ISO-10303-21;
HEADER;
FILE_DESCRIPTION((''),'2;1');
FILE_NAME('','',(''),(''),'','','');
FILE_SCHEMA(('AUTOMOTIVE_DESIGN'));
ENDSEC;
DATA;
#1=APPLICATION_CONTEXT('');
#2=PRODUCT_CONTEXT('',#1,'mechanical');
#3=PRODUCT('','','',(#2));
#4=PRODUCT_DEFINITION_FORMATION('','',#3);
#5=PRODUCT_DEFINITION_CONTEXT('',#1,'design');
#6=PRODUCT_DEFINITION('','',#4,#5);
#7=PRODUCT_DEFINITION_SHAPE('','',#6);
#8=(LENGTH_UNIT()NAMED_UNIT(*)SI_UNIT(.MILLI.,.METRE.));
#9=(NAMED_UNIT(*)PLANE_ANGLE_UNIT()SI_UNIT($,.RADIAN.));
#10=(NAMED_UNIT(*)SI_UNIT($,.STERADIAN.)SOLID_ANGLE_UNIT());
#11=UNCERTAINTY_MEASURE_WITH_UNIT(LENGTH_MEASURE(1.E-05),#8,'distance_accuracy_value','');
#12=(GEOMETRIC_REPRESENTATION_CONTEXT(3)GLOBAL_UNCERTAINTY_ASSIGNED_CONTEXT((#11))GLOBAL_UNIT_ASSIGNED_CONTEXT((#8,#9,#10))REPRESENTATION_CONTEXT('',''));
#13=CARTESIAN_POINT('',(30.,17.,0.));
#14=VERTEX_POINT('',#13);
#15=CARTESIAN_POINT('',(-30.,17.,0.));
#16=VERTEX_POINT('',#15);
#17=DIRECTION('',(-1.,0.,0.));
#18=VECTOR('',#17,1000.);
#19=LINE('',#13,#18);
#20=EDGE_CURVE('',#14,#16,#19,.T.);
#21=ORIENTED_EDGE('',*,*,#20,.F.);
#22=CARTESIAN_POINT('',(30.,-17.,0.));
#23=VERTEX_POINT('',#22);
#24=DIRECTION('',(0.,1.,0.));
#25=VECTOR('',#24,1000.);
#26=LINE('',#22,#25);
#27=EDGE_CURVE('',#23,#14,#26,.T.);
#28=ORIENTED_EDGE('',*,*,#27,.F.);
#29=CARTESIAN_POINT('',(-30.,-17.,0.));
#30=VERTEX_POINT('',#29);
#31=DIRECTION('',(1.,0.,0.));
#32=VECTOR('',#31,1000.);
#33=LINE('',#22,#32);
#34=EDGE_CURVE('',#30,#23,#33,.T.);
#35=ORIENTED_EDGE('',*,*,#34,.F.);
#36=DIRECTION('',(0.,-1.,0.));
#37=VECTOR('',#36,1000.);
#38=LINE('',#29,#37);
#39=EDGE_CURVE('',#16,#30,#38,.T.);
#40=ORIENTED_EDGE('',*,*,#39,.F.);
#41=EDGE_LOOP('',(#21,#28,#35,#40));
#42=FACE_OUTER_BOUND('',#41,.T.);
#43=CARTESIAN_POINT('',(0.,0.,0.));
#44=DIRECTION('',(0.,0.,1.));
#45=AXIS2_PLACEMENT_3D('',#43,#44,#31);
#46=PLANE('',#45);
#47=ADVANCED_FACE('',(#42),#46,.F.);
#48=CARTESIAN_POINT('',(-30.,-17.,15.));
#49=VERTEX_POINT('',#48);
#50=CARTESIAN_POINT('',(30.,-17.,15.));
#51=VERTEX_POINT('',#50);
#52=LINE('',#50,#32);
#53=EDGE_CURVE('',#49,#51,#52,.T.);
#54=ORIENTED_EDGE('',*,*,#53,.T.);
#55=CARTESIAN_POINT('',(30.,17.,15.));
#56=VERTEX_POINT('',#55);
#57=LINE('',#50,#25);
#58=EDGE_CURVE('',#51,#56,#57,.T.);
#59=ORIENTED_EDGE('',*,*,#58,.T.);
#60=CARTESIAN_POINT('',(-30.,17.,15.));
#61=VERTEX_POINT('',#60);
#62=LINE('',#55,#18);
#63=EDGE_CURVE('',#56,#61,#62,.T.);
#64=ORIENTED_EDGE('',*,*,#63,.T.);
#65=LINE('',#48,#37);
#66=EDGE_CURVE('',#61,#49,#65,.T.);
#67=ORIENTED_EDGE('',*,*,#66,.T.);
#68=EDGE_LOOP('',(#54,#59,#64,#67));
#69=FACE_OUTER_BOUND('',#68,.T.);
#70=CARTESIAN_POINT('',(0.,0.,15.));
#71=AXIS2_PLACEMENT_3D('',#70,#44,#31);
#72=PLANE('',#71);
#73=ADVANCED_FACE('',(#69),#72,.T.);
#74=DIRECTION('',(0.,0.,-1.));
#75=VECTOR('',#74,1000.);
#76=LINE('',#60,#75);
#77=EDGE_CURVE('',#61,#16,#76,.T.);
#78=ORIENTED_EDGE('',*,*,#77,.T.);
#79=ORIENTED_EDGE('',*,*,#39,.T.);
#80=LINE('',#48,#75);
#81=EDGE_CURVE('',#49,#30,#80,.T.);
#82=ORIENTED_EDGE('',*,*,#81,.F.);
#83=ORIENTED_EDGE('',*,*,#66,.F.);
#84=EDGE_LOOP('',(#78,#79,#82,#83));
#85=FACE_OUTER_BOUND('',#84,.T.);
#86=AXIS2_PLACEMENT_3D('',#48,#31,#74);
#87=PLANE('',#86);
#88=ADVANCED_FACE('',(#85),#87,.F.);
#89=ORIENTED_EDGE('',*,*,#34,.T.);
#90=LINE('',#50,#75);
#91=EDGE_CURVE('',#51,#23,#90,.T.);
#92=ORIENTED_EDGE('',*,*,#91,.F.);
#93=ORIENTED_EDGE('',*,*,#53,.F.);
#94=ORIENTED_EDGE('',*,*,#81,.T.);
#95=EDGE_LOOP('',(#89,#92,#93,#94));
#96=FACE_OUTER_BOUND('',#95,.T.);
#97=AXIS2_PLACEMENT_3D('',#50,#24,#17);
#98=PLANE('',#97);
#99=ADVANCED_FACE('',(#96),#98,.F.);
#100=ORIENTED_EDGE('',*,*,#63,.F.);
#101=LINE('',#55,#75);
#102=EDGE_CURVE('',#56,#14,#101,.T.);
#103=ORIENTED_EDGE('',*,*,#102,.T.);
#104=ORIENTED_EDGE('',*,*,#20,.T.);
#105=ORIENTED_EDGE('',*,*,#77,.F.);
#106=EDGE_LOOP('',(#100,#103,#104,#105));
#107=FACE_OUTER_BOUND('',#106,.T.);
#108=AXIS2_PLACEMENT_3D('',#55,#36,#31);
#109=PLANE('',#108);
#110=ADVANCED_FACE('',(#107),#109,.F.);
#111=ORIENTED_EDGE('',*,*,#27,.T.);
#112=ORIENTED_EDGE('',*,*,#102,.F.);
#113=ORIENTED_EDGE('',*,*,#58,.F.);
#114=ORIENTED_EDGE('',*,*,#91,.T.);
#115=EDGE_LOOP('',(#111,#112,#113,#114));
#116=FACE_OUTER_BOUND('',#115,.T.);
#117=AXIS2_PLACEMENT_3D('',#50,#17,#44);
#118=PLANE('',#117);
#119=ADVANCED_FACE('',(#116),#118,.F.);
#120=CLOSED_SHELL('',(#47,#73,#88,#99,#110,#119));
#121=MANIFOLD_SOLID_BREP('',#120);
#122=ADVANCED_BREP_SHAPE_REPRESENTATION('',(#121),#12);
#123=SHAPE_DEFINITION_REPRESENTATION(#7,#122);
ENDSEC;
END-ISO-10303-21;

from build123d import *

# Parameters (mm, degrees)
SKETCH_1_W      = 60
SKETCH_1_H      = 34
EXTRUDE_1_DEPTH = 15


with BuildPart() as part:
    # 草图1 → 凸台-拉伸1 (new body)
    with BuildSketch(Plane.XY):
        Rectangle(SKETCH_1_W, SKETCH_1_H)
    extrude(amount=EXTRUDE_1_DEPTH)


solid = part.part
